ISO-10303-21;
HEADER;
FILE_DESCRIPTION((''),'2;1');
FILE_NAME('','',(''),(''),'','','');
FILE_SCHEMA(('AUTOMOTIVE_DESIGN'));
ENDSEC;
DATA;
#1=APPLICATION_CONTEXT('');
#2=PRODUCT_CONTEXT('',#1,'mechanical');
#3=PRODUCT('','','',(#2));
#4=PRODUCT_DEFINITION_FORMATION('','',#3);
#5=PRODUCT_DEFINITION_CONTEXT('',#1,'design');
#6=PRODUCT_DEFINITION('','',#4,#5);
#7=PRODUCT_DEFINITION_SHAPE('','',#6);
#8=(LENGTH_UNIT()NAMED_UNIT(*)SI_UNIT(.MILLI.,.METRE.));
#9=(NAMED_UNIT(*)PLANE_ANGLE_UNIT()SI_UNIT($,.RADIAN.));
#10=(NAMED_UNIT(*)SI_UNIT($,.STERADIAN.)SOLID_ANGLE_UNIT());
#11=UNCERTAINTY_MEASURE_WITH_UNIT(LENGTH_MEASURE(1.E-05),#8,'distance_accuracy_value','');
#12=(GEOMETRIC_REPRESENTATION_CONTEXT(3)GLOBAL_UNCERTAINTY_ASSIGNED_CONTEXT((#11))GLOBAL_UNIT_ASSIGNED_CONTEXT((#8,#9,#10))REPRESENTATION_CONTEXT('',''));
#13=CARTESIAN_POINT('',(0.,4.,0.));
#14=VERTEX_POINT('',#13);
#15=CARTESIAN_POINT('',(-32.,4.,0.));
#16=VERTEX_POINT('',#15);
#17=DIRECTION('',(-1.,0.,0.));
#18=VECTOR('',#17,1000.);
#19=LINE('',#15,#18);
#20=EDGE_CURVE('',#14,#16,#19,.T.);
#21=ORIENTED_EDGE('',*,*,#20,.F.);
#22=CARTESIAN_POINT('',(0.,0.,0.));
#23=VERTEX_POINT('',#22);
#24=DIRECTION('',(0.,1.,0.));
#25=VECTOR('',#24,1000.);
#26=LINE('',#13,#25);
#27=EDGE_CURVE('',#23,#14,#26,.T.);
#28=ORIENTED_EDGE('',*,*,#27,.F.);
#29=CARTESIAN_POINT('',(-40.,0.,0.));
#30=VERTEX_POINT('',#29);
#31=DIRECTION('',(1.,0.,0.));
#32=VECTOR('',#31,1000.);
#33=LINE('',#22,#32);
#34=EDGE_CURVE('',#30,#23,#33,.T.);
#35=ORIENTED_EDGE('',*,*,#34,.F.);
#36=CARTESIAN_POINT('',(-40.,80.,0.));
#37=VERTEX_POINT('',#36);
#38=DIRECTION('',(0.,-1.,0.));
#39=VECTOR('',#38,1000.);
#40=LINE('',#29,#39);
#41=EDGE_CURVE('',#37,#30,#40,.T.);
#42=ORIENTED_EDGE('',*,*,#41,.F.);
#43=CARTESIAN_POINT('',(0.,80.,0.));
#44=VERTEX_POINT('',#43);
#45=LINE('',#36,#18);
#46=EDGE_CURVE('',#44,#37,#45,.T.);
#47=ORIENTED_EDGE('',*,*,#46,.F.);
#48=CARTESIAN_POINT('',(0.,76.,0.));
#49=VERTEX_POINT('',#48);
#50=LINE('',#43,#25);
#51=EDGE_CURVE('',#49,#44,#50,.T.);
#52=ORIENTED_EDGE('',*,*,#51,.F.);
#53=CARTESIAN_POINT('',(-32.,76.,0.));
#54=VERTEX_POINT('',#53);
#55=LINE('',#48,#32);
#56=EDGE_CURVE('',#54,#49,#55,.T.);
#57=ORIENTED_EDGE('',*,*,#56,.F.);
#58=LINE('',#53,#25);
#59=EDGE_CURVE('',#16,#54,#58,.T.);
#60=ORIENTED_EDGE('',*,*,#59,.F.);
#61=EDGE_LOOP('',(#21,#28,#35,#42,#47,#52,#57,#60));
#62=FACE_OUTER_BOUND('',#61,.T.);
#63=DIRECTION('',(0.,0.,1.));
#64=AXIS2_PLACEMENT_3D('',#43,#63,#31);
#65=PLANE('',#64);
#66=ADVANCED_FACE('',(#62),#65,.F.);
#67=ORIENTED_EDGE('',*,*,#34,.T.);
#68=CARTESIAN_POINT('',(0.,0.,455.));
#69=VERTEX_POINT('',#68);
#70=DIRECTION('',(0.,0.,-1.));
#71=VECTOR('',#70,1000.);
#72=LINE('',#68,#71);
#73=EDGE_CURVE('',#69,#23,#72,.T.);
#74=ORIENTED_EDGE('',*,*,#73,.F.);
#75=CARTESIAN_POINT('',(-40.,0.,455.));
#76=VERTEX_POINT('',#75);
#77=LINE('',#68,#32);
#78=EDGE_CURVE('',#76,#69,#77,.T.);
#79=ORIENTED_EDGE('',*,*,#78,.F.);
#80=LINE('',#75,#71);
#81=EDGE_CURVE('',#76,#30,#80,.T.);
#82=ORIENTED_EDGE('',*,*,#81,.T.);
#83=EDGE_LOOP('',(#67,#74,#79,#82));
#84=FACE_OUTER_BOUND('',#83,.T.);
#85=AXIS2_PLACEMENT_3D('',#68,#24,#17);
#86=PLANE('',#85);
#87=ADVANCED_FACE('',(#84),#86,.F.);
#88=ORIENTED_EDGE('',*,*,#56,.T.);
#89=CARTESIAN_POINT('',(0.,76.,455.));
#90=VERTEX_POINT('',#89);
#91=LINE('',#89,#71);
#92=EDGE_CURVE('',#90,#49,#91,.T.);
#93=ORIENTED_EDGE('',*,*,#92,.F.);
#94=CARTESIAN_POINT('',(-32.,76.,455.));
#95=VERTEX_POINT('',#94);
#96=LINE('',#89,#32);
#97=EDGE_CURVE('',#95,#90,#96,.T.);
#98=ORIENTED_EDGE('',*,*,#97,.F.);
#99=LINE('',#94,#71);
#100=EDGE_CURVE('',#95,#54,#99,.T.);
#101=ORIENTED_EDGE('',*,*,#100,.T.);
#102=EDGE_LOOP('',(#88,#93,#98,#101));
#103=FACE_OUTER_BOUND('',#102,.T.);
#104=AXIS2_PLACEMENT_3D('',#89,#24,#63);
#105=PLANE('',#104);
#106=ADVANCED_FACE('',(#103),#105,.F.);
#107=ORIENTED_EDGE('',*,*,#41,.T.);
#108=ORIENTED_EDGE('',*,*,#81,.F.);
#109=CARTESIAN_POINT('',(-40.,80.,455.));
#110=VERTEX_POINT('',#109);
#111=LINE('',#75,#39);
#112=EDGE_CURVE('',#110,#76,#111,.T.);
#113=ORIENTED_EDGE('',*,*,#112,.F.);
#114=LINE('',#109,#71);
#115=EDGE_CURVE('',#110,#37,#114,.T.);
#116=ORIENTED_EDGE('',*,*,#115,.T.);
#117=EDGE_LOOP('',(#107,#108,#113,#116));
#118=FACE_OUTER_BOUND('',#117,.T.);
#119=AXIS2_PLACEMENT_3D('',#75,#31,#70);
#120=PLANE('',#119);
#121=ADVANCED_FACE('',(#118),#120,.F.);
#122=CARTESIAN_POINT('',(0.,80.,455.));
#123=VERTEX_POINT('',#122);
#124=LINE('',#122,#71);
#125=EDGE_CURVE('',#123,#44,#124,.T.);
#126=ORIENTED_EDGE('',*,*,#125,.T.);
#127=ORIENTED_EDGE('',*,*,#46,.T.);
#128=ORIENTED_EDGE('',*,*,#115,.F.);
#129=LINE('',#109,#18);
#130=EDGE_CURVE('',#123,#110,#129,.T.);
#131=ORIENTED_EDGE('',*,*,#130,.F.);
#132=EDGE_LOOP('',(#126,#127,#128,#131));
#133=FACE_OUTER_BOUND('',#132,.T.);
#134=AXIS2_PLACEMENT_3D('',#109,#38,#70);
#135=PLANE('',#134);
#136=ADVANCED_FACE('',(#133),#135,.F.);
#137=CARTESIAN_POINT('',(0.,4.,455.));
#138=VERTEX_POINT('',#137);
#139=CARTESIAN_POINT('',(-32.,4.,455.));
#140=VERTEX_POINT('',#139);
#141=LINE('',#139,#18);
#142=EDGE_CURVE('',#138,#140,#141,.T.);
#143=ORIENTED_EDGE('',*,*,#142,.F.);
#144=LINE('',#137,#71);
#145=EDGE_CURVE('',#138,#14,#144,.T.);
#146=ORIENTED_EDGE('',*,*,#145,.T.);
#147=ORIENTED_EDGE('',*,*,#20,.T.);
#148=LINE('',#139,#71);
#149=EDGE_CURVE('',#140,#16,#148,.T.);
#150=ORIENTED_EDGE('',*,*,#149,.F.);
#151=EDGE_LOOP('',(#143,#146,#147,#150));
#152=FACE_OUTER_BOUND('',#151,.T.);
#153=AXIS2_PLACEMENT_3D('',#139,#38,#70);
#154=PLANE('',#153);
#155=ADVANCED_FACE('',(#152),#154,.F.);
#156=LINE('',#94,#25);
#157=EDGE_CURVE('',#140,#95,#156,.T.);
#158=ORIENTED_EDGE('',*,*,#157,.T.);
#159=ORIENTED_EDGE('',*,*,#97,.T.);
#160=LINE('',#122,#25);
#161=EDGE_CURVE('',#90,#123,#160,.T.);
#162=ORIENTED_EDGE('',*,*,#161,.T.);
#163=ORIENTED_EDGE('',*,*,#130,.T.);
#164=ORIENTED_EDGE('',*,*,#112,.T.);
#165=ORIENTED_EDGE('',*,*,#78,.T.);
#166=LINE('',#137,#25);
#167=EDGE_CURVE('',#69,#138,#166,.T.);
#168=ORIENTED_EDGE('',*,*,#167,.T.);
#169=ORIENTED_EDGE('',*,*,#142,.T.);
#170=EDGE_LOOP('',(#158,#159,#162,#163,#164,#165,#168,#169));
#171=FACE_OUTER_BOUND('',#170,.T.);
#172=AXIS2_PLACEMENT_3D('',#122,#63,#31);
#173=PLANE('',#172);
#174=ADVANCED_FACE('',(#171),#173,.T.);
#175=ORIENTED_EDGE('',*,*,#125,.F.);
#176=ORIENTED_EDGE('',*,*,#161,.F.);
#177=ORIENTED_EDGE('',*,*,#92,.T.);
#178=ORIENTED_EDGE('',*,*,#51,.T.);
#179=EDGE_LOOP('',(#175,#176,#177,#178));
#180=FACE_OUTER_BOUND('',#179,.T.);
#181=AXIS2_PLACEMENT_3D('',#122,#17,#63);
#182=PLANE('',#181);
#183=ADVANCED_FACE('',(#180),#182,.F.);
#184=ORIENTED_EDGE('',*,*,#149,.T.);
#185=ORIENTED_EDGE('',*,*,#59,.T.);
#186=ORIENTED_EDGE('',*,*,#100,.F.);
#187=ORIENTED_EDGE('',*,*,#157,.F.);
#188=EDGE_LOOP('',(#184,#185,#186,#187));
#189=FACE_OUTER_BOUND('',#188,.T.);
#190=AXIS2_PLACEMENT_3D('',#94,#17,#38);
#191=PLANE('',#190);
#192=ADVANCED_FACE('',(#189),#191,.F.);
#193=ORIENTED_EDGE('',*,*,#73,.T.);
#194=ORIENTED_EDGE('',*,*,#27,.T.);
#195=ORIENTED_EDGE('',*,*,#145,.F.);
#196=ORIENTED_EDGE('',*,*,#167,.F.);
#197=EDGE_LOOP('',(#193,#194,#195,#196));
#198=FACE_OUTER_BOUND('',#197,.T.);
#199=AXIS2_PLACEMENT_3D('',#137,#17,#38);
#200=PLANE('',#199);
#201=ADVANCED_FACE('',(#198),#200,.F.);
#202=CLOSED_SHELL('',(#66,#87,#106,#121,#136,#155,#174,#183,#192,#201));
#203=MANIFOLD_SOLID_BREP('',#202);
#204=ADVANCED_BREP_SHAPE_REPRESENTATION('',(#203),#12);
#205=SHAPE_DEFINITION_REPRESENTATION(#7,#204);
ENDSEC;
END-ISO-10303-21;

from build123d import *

# Parameters (mm, degrees)
EXTRUDE1_DEPTH = 455


with BuildPart() as part:
    # Sketch1 → Extrude1 (new body)
    with BuildSketch(Plane.XY):
        Polygon((0, 0), (-40, 0), (-40, 80), (0, 80), (0, 76), (-32, 76), (-32, 4), (0, 4), align=None)
    extrude(amount=EXTRUDE1_DEPTH)


solid = part.part
